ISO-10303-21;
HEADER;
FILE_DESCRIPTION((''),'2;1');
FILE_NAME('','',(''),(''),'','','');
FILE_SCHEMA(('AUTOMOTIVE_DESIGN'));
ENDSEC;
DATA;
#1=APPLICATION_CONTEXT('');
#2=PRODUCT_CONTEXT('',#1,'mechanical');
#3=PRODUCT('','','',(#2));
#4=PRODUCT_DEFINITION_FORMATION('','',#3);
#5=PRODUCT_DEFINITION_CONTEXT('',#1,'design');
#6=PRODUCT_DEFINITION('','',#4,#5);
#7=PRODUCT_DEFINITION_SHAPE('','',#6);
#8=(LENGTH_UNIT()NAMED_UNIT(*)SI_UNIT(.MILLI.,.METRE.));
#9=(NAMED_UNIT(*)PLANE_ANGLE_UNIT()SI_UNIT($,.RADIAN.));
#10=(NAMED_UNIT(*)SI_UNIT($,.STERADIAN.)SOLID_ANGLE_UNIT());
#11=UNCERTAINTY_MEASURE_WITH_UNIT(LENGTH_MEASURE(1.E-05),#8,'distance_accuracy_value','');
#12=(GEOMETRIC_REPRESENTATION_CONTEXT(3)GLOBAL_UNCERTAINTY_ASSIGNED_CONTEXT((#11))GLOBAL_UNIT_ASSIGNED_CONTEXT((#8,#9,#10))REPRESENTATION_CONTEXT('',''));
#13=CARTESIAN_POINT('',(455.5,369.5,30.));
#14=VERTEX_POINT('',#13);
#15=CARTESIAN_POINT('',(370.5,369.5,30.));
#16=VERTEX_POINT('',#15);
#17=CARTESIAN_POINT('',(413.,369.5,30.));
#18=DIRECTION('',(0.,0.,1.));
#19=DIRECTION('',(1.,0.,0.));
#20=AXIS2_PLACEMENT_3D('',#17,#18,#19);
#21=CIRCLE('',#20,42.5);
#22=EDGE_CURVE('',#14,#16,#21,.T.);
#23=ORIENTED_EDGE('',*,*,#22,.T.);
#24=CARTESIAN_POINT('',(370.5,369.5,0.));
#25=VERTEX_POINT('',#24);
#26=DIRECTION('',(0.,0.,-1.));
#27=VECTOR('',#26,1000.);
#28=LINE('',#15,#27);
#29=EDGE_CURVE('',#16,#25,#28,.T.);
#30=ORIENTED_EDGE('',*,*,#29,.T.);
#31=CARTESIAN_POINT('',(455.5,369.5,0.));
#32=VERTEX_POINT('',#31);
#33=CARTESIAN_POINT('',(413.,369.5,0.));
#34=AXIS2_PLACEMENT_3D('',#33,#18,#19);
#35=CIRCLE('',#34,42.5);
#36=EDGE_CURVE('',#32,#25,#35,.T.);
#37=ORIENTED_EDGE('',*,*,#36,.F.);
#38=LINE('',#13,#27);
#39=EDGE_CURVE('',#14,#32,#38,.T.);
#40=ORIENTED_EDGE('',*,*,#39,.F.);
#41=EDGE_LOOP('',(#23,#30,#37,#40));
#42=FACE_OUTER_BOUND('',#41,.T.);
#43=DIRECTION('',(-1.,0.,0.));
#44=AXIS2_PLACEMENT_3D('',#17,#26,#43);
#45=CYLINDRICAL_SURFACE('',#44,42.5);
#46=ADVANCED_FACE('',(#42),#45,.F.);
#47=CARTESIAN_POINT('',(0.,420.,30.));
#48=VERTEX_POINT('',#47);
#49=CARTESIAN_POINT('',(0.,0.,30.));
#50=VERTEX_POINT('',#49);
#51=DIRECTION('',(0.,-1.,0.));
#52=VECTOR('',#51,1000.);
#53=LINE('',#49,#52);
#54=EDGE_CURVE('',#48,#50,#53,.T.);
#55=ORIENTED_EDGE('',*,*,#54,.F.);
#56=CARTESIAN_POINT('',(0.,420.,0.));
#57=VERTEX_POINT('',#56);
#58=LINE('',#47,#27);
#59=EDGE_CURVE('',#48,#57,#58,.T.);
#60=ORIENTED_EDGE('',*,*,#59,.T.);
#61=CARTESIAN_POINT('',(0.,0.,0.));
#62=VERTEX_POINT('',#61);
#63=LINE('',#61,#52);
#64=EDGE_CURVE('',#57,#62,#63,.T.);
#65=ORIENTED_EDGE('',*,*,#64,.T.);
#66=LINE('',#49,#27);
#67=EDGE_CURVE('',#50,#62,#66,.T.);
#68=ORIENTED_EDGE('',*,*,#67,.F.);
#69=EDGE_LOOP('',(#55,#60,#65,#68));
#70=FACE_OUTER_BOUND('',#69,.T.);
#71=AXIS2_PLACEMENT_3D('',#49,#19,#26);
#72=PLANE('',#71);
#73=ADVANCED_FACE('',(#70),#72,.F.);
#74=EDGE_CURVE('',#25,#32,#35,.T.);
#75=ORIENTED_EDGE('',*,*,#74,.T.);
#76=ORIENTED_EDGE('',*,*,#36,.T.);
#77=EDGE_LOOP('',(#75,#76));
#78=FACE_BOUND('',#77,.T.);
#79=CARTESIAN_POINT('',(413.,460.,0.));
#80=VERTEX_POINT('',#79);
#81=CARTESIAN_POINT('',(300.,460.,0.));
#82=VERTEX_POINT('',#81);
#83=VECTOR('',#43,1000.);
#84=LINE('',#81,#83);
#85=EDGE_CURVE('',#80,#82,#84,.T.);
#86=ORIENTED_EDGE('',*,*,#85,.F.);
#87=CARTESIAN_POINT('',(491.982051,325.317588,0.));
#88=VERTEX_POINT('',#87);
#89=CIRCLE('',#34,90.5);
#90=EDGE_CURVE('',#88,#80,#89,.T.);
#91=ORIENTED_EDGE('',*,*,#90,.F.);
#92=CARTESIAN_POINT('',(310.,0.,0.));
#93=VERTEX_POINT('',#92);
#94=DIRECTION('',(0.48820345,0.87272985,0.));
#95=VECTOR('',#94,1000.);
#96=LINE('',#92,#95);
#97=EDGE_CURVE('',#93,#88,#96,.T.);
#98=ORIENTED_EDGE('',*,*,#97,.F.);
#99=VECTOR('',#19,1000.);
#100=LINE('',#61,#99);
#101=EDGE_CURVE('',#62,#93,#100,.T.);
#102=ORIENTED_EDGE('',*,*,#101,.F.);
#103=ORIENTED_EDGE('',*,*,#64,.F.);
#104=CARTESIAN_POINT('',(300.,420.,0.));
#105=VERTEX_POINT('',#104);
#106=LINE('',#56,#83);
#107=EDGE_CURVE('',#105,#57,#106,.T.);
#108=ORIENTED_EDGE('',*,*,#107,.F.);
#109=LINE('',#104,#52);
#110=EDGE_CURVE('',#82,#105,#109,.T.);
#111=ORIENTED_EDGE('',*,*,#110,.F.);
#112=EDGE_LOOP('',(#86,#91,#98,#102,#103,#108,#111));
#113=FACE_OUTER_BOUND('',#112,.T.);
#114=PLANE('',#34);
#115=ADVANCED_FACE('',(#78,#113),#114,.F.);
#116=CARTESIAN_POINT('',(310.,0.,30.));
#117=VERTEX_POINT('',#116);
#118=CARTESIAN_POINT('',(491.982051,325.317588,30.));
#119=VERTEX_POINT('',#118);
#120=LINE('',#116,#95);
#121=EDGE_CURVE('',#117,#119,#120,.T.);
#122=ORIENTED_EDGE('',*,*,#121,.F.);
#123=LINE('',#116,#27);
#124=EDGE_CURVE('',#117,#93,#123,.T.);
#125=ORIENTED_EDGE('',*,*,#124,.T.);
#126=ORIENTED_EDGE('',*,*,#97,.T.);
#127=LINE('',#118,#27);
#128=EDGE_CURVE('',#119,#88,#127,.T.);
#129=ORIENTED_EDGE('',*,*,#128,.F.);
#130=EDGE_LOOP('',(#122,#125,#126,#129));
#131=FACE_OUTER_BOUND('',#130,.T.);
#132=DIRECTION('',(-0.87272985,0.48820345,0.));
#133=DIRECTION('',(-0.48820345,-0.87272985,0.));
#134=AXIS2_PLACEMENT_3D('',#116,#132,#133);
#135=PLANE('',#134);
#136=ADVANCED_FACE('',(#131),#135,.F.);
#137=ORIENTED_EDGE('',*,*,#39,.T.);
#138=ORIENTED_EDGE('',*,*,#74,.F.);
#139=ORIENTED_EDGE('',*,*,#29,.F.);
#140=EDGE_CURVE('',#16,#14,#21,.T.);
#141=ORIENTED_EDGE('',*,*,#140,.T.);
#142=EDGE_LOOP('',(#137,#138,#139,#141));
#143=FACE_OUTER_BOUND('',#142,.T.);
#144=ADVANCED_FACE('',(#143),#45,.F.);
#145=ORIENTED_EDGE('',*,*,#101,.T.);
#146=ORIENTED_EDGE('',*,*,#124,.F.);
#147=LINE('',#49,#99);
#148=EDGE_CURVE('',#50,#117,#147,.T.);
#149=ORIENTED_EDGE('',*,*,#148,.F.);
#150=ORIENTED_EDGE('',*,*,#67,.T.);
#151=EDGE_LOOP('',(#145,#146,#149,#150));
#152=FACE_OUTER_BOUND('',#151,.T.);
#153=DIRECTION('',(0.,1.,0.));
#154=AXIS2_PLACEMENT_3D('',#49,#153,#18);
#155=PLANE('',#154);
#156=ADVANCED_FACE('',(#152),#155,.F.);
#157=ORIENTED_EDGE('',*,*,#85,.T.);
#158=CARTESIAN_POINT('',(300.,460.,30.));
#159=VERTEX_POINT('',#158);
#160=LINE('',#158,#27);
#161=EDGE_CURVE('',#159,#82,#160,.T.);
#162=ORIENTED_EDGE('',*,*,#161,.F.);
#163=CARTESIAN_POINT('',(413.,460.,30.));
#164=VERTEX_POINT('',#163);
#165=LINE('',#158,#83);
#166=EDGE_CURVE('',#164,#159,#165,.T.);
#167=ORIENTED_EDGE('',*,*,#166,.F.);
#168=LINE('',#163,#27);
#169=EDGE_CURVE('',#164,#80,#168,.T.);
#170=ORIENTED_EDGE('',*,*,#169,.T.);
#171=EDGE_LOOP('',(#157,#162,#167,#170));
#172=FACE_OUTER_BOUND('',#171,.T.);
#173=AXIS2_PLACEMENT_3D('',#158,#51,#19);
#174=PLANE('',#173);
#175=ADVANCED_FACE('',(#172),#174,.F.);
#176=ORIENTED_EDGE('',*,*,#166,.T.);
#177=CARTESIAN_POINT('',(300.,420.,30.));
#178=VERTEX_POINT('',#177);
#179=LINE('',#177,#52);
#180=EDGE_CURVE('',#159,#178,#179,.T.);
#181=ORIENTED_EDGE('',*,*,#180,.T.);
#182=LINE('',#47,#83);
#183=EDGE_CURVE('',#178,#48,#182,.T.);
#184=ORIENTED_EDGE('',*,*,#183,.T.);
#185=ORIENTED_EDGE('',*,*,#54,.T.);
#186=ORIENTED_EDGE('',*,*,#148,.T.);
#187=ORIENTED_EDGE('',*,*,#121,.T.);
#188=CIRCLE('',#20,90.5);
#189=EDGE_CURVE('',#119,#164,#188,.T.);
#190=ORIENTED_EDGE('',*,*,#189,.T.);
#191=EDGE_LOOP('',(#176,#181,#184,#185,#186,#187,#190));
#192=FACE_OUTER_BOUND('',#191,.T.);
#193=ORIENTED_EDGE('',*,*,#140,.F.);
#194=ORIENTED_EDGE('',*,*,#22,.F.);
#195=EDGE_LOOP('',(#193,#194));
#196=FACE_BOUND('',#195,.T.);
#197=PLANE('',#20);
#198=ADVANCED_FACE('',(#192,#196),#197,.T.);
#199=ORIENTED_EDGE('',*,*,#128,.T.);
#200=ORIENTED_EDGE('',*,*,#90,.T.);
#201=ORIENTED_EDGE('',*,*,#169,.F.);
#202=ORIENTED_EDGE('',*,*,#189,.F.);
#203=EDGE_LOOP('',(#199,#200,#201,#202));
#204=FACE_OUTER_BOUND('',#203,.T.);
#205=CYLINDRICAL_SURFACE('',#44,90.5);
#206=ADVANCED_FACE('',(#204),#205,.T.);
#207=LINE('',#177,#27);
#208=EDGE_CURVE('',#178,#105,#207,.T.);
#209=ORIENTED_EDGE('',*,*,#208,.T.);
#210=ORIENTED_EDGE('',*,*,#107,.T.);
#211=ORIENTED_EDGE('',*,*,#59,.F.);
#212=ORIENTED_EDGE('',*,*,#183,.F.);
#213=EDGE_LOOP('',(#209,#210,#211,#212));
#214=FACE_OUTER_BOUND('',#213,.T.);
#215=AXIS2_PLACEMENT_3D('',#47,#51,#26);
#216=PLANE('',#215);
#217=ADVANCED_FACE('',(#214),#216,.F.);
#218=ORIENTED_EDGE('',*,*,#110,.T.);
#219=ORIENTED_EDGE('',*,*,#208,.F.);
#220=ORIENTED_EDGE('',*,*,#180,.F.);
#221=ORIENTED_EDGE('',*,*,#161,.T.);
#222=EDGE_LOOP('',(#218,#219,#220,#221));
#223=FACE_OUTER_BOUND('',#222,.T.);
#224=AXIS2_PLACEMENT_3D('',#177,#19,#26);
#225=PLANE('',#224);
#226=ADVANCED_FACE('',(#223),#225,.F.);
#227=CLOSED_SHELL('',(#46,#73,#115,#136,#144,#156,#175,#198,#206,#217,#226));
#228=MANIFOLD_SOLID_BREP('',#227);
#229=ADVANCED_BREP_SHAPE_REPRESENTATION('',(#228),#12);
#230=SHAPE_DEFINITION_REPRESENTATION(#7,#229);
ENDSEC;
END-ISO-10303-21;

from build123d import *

# Parameters (mm, degrees)
SKETCH1_R           = 42.5
BOSS_EXTRUDE1_DEPTH = 30


with BuildPart() as part:
    # Sketch1 → Boss-Extrude1 (new body)
    with BuildSketch(Plane.XY):
        with BuildLine():
            Line((0, 0), (0, 420))
            Line((0, 420), (300, 420))
            Line((300, 420), (300, 460))
            Line((300, 460), (413, 460))
            ThreePointArc((413, 460), (491.066504669, 415.280682048), (491.982051466, 325.317587819))
            Line((491.982051466, 325.317587819), (310, 0))
            Line((310, 0), (0, 0))
        make_face()
        with Locations((413, 369.5)):
            Circle(SKETCH1_R, mode=Mode.SUBTRACT)
    extrude(amount=BOSS_EXTRUDE1_DEPTH)


solid = part.part
